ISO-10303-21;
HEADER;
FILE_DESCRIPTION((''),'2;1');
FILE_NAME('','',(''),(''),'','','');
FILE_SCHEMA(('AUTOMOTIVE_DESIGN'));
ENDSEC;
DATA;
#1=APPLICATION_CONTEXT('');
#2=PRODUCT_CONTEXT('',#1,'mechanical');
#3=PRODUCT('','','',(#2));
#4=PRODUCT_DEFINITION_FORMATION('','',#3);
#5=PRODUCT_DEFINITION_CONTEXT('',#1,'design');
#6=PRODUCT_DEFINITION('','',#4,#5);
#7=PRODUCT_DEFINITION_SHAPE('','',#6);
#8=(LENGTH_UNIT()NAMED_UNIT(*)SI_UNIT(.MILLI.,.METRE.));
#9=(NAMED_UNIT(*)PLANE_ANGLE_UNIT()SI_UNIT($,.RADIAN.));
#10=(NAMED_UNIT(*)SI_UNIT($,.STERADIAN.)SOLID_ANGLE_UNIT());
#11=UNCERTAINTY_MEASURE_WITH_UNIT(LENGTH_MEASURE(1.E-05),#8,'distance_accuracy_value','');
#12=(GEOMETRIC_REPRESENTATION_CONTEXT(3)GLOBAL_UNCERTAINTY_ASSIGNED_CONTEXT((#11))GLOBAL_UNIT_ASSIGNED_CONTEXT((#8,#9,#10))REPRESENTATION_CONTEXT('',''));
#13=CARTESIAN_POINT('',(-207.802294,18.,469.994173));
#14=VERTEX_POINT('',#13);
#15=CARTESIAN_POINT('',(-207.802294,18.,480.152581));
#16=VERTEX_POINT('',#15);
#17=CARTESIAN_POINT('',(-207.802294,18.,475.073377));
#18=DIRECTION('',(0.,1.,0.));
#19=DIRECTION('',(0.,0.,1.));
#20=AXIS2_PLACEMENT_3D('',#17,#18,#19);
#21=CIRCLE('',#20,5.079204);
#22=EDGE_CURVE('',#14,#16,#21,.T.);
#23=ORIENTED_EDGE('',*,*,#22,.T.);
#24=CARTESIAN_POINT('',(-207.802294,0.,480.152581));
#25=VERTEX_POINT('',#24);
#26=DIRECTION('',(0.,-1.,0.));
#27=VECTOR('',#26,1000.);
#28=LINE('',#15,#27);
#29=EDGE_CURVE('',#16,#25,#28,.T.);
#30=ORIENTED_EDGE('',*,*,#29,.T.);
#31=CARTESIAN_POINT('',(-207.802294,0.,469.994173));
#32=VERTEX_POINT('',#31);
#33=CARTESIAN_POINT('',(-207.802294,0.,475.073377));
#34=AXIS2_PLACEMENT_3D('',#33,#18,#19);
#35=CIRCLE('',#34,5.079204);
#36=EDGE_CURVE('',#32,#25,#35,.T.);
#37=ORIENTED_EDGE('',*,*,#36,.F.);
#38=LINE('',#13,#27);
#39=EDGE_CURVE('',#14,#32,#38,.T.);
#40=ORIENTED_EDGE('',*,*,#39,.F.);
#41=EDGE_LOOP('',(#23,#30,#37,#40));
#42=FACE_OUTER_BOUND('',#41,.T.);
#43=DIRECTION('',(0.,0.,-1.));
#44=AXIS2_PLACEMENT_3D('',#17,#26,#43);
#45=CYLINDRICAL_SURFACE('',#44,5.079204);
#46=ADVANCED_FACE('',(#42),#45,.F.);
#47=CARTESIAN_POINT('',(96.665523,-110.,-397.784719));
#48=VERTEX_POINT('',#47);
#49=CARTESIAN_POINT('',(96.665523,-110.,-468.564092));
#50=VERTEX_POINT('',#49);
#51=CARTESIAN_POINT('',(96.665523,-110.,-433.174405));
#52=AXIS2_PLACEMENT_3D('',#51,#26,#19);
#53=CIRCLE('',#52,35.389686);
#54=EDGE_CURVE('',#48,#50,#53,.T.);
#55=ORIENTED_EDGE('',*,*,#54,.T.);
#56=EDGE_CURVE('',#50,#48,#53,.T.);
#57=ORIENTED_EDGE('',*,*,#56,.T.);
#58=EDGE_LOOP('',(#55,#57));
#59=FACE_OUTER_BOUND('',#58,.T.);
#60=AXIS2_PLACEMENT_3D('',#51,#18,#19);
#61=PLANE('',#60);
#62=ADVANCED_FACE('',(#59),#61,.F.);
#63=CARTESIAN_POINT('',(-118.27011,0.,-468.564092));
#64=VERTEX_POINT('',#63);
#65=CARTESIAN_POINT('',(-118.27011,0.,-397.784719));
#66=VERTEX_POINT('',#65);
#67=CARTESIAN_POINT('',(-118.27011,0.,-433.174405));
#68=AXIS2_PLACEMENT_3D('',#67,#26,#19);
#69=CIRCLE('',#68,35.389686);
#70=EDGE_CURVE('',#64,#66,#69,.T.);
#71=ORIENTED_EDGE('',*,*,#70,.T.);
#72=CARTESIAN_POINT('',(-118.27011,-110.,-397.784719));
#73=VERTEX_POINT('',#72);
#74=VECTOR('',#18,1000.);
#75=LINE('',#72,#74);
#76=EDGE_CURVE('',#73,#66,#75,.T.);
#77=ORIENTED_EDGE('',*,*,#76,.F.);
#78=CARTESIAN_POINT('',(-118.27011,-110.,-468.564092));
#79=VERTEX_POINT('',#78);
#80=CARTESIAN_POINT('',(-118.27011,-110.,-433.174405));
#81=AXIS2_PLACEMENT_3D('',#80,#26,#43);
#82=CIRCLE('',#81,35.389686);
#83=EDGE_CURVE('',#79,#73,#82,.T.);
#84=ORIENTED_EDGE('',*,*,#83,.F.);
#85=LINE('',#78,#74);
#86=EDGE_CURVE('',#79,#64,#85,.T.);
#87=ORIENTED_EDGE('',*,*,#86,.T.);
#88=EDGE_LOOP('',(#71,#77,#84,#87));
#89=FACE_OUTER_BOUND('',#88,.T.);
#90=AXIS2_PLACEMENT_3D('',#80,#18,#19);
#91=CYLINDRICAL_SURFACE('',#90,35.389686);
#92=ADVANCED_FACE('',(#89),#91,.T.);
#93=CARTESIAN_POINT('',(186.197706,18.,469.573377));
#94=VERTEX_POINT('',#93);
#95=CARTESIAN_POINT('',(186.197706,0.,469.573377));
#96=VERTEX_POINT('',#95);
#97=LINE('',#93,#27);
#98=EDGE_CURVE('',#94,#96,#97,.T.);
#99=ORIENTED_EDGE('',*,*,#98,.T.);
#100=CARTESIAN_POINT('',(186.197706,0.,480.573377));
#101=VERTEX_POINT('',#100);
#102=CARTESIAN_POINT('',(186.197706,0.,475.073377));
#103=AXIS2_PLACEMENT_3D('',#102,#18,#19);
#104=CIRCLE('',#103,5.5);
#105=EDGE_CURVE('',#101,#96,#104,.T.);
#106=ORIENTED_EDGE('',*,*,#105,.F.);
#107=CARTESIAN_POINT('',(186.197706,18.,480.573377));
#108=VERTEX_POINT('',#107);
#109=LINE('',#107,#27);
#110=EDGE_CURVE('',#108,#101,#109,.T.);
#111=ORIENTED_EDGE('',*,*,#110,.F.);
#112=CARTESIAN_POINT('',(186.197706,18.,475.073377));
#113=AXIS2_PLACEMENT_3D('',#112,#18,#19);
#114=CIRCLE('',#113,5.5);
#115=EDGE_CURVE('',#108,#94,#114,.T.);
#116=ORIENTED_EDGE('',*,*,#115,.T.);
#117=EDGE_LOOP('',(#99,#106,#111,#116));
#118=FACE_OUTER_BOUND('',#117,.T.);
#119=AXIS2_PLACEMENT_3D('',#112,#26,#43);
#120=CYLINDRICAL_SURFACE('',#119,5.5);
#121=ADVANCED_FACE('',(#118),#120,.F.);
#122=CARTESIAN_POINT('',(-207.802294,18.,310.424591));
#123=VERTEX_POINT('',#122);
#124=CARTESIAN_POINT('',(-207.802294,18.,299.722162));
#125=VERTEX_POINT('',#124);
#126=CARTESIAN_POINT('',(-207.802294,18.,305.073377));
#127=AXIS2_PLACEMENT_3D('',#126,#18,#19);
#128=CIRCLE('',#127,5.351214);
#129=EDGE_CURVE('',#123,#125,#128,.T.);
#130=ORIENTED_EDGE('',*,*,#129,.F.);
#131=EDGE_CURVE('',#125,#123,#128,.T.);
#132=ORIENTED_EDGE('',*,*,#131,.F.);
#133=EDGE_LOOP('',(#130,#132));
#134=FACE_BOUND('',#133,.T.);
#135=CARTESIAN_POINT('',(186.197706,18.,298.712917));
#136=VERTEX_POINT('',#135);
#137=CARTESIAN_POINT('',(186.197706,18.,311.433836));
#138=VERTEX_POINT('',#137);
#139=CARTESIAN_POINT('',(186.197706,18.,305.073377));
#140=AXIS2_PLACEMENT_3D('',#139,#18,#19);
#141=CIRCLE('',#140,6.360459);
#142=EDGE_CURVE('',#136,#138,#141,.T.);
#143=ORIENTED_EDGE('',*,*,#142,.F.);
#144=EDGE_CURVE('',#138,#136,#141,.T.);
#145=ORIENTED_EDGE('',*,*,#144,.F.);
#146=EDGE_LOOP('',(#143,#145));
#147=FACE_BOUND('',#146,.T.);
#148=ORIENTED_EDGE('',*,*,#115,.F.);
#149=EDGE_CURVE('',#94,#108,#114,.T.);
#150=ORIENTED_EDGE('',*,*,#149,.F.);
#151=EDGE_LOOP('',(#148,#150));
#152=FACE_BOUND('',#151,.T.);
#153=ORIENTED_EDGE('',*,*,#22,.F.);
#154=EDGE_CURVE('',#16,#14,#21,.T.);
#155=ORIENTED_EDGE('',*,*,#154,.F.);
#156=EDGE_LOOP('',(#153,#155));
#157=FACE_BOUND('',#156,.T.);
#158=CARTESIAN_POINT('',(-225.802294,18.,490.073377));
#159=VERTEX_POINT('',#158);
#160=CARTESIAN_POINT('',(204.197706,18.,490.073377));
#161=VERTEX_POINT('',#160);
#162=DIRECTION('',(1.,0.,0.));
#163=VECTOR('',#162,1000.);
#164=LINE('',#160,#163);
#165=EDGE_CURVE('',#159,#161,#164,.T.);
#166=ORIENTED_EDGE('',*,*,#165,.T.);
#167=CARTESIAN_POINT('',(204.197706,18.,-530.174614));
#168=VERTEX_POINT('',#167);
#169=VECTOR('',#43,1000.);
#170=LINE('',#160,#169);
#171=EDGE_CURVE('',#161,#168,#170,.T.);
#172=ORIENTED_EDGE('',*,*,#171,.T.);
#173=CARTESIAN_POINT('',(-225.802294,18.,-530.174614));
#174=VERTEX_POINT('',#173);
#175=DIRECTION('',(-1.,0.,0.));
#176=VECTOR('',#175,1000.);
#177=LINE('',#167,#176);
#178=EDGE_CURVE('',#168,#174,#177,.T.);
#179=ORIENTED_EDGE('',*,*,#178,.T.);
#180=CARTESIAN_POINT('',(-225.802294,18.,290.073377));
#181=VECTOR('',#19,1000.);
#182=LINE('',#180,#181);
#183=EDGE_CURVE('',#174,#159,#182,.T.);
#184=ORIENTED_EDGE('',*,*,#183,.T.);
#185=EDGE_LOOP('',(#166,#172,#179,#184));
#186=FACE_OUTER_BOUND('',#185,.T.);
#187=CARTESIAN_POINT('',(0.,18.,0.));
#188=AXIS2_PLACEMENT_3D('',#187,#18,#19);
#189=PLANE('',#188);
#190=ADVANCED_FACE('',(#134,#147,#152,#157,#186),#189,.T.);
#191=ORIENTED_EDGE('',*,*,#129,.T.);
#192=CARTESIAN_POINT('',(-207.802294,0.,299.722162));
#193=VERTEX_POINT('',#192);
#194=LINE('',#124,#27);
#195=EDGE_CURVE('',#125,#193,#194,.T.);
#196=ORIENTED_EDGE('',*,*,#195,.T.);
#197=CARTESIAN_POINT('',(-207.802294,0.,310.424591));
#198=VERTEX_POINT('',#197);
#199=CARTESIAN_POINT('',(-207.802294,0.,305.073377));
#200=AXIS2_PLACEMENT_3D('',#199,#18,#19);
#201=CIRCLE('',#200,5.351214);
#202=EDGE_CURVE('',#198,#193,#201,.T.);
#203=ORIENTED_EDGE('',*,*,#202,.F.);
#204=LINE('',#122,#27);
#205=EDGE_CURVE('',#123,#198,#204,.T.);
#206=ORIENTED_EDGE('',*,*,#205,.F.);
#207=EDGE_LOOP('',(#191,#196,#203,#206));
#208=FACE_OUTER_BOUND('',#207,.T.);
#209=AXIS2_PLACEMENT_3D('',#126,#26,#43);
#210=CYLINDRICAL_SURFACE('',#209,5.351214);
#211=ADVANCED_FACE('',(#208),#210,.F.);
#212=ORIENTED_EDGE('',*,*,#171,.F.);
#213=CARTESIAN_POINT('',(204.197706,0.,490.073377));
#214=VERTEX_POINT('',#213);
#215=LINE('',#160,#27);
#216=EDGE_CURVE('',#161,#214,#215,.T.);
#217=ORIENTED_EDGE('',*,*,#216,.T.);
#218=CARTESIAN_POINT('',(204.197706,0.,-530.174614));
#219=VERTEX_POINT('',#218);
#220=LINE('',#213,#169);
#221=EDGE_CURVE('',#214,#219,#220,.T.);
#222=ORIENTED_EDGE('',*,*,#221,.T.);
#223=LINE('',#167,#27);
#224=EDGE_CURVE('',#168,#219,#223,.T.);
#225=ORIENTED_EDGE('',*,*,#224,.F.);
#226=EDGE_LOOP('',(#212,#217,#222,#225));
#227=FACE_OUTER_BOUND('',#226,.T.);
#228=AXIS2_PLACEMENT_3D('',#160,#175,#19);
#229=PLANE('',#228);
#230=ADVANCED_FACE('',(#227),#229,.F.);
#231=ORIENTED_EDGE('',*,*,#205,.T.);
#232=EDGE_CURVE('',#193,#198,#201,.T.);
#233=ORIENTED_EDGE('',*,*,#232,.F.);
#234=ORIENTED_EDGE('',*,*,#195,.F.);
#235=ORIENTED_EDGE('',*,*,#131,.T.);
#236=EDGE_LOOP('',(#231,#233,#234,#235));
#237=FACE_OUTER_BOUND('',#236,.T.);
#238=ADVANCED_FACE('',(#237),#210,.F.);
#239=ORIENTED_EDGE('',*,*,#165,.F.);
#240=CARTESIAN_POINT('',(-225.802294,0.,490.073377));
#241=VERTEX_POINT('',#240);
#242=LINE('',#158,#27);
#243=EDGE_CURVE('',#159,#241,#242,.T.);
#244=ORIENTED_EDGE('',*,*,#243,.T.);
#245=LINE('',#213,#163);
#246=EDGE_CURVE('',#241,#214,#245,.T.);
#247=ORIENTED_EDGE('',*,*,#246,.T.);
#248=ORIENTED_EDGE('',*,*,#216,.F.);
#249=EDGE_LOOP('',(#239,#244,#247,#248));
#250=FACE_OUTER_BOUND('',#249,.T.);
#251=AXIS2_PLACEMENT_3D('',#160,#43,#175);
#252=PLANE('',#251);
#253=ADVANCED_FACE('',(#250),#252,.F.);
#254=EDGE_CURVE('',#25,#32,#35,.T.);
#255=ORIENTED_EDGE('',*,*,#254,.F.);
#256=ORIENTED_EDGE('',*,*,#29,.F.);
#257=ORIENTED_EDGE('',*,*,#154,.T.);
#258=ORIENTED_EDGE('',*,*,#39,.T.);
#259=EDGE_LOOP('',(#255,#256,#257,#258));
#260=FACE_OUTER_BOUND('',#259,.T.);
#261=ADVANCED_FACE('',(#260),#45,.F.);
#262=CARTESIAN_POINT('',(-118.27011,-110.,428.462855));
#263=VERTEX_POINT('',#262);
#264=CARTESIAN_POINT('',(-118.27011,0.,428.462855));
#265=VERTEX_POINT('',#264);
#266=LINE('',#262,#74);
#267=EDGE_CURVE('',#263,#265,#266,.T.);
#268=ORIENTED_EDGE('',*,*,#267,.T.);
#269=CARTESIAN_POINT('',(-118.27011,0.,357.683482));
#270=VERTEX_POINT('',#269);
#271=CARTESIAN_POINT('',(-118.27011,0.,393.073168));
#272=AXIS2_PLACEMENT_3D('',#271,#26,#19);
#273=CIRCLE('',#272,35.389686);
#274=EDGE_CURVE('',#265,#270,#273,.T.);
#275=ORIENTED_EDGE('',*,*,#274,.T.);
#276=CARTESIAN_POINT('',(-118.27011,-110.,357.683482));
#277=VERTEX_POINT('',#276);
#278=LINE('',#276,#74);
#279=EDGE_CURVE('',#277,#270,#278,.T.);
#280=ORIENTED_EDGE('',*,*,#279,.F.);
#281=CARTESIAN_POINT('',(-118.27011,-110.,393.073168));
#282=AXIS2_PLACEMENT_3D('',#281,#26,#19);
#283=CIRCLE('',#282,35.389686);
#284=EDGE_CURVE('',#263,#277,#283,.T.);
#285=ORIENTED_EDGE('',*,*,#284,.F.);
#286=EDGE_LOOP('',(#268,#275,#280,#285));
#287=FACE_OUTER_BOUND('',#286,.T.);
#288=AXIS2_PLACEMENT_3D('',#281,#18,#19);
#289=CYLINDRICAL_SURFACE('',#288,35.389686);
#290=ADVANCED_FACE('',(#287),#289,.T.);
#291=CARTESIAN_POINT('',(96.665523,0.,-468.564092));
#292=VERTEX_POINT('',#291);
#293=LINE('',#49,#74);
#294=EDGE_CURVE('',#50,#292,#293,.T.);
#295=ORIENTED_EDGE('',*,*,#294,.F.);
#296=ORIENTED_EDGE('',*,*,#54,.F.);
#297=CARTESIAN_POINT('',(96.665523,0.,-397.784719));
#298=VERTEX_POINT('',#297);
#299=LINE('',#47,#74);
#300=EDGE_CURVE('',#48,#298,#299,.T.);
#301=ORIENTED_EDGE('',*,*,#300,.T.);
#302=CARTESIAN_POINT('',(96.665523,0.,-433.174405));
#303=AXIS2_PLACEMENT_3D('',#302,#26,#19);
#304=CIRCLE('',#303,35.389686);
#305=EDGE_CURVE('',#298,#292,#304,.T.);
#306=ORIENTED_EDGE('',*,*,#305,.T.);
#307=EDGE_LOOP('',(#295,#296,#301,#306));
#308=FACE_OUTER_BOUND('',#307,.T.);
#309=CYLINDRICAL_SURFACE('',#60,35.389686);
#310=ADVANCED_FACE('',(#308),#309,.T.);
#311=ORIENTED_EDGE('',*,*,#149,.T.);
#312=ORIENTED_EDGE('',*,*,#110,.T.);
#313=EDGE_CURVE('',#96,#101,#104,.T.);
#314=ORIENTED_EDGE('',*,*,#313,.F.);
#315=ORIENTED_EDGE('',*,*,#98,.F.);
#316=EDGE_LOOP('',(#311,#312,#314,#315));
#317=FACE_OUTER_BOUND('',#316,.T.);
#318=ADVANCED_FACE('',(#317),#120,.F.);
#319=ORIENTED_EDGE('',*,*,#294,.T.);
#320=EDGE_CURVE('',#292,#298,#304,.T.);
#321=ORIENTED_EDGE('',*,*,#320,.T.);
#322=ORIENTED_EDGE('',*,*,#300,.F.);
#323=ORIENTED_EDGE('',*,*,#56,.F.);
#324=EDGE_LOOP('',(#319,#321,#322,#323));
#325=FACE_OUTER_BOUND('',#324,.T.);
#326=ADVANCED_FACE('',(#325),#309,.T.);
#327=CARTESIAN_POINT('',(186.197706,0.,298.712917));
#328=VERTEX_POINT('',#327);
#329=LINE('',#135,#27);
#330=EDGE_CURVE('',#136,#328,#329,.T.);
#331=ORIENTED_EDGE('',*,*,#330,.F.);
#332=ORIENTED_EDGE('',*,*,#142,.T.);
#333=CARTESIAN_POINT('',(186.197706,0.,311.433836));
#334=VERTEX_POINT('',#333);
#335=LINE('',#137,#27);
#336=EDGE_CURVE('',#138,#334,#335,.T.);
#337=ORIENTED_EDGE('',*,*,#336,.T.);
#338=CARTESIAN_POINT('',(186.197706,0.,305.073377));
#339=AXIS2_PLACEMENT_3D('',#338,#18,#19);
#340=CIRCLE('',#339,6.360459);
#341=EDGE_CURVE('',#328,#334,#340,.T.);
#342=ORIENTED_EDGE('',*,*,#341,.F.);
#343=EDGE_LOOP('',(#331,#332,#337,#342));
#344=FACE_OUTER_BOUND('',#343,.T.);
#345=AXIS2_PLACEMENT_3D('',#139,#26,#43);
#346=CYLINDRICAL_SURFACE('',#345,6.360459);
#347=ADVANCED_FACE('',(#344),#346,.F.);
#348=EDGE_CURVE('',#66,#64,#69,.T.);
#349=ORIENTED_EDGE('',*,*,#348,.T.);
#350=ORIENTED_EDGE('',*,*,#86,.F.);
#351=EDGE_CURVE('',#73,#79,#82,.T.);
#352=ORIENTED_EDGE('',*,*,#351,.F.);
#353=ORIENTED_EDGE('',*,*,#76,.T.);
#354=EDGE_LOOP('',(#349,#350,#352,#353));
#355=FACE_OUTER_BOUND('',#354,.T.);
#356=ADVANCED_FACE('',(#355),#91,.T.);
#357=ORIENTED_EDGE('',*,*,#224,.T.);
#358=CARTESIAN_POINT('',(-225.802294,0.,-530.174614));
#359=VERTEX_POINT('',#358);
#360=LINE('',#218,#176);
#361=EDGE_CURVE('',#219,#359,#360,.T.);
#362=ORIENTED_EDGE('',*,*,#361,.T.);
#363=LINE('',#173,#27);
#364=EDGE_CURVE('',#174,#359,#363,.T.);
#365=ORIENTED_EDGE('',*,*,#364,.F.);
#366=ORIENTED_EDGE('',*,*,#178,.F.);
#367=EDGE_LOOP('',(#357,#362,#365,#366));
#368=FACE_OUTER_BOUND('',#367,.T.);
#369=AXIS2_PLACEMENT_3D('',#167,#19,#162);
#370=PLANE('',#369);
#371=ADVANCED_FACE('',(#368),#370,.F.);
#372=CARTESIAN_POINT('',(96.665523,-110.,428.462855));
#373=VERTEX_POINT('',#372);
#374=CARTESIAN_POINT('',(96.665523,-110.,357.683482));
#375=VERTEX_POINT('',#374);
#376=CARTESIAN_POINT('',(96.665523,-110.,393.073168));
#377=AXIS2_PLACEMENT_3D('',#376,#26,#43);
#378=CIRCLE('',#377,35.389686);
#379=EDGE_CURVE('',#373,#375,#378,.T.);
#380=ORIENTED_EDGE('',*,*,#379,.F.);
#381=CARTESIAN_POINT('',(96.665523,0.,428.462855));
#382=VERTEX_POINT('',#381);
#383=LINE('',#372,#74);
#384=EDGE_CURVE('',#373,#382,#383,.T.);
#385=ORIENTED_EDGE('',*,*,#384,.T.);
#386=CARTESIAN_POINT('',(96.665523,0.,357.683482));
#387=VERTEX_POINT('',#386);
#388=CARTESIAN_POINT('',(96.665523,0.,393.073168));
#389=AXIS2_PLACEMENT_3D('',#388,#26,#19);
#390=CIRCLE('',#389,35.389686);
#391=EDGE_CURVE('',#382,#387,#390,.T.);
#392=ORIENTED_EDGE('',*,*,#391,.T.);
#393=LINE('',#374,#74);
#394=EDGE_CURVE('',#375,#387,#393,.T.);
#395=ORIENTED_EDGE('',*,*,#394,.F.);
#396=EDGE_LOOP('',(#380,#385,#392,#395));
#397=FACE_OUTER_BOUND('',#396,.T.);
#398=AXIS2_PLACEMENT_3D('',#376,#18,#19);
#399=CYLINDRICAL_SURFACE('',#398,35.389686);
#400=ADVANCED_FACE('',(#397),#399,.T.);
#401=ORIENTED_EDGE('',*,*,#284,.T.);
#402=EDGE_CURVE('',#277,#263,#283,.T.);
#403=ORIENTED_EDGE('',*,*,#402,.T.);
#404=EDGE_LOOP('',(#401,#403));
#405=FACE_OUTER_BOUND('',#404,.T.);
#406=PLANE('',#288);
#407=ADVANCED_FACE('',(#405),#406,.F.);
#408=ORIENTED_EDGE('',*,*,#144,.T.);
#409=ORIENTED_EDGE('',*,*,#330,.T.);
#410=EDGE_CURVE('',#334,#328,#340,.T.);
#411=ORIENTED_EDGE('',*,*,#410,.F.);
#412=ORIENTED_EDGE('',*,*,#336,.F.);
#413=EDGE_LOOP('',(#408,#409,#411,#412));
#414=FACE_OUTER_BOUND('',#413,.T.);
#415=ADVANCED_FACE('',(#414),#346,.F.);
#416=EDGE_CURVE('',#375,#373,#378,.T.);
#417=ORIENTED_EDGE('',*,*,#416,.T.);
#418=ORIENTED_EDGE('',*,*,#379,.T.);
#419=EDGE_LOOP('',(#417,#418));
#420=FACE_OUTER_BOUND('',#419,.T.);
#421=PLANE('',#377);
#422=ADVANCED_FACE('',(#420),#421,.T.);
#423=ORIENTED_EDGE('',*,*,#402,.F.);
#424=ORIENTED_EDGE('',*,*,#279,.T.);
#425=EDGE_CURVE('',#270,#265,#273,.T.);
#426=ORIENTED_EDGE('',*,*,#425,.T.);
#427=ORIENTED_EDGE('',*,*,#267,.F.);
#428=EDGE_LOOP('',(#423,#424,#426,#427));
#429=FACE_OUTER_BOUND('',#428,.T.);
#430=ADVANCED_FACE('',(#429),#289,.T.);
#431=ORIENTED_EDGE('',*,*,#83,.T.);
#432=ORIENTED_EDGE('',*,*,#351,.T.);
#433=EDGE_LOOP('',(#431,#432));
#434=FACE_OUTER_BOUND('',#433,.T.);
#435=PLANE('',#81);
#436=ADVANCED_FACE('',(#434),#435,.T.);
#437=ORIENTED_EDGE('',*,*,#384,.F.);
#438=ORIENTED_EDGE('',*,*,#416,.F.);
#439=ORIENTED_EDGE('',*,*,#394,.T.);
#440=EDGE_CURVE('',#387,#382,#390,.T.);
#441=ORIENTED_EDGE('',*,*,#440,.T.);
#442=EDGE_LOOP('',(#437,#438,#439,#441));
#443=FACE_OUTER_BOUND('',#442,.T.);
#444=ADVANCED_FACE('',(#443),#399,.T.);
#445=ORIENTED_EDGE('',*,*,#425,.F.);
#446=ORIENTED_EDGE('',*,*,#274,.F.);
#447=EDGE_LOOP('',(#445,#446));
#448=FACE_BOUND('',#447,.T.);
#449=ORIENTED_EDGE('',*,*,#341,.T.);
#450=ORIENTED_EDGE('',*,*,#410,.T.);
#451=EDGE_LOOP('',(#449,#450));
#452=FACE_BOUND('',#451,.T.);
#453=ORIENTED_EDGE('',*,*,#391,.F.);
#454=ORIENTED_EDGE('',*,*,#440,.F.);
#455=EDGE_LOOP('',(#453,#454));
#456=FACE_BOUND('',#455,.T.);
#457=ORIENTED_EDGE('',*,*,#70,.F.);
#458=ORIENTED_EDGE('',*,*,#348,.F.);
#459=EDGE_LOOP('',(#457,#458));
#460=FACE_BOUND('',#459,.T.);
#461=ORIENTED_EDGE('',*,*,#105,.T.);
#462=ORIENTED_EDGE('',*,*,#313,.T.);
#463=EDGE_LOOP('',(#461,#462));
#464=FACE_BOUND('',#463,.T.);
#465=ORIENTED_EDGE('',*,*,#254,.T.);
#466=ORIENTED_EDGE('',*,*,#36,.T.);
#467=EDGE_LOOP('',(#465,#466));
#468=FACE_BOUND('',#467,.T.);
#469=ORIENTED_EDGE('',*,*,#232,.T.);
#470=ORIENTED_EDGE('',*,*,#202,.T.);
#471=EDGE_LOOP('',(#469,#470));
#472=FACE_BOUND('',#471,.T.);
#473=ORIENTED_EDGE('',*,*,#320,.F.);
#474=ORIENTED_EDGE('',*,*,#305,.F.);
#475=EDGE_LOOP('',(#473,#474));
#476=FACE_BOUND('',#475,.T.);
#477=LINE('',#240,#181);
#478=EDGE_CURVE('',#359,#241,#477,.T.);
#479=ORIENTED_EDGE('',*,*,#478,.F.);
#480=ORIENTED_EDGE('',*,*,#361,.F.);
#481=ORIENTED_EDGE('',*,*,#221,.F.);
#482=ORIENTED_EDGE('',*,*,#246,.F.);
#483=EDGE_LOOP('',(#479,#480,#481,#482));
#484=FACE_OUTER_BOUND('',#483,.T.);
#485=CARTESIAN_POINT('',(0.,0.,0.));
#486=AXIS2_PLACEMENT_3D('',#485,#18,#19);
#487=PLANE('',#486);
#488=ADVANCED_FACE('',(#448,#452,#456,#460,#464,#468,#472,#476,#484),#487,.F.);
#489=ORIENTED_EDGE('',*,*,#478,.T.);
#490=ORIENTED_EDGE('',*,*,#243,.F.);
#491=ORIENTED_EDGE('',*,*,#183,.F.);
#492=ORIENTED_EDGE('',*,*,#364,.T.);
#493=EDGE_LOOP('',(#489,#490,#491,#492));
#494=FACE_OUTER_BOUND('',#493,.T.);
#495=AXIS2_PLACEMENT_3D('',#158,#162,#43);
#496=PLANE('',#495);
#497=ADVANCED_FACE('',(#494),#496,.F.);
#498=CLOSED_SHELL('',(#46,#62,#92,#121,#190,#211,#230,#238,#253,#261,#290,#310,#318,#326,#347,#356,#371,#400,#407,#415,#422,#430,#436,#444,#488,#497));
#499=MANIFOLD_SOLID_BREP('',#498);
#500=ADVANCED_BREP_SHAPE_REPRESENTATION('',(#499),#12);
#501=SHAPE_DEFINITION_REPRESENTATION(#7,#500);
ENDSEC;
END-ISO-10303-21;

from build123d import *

# Parameters (mm, degrees)
SKETCH1_R           = 5.5
SKETCH1_R_2         = 6.36045924
SKETCH1_R_3         = 5.351214453
SKETCH1_R_4         = 5.079203988
BOSS_EXTRUDE1_DEPTH = 18
SKETCH2_R           = 35.389686151
BOSS_EXTRUDE2_DEPTH = 110


with BuildPart() as part:
    # Sketch1 → Boss-Extrude1 (new body)
    with BuildSketch(Plane(origin=(0, 0, 0), x_dir=(1, 0, 0), z_dir=(0, 1, 0))):
        Polygon((204.197706314, -490.073376619), (-225.802293686, -490.073376619), (-225.802293686, -290.073376619), (-225.802293686, 530.17461365), (204.197706314, 530.17461365), align=None)
        with Locations(Location((186.197706314, -475.073376619, 0), (0, 0, 270))):
            Circle(SKETCH1_R, mode=Mode.SUBTRACT)
        with Locations(Location((186.197706314, -305.073376619, 0), (0, 0, 270))):
            Circle(SKETCH1_R_2, mode=Mode.SUBTRACT)
        with Locations(Location((-207.802293686, -305.073376619, 0), (0, 0, 270))):
            Circle(SKETCH1_R_3, mode=Mode.SUBTRACT)
        with Locations(Location((-207.802293686, -475.073376619, 0), (0, 0, 270))):
            Circle(SKETCH1_R_4, mode=Mode.SUBTRACT)
    extrude(amount=BOSS_EXTRUDE1_DEPTH)

    # Sketch2 → Boss-Extrude2 (add)
    with BuildSketch(Plane.XZ):
        with Locations(Location((96.665522834, 393.073168436, 0), (0, 0, 90))):
            Circle(SKETCH2_R)
        with Locations(Location((-118.270110206, 393.073168436, 0), (0, 0, 90))):
            Circle(SKETCH2_R)
        with Locations(Location((-118.270110206, -433.174405466, 0), (0, 0, 90))):
            Circle(SKETCH2_R)
        with Locations(Location((96.665522834, -433.174405466, 0), (0, 0, 90))):
            Circle(SKETCH2_R)
    extrude(amount=BOSS_EXTRUDE2_DEPTH)


solid = part.part
